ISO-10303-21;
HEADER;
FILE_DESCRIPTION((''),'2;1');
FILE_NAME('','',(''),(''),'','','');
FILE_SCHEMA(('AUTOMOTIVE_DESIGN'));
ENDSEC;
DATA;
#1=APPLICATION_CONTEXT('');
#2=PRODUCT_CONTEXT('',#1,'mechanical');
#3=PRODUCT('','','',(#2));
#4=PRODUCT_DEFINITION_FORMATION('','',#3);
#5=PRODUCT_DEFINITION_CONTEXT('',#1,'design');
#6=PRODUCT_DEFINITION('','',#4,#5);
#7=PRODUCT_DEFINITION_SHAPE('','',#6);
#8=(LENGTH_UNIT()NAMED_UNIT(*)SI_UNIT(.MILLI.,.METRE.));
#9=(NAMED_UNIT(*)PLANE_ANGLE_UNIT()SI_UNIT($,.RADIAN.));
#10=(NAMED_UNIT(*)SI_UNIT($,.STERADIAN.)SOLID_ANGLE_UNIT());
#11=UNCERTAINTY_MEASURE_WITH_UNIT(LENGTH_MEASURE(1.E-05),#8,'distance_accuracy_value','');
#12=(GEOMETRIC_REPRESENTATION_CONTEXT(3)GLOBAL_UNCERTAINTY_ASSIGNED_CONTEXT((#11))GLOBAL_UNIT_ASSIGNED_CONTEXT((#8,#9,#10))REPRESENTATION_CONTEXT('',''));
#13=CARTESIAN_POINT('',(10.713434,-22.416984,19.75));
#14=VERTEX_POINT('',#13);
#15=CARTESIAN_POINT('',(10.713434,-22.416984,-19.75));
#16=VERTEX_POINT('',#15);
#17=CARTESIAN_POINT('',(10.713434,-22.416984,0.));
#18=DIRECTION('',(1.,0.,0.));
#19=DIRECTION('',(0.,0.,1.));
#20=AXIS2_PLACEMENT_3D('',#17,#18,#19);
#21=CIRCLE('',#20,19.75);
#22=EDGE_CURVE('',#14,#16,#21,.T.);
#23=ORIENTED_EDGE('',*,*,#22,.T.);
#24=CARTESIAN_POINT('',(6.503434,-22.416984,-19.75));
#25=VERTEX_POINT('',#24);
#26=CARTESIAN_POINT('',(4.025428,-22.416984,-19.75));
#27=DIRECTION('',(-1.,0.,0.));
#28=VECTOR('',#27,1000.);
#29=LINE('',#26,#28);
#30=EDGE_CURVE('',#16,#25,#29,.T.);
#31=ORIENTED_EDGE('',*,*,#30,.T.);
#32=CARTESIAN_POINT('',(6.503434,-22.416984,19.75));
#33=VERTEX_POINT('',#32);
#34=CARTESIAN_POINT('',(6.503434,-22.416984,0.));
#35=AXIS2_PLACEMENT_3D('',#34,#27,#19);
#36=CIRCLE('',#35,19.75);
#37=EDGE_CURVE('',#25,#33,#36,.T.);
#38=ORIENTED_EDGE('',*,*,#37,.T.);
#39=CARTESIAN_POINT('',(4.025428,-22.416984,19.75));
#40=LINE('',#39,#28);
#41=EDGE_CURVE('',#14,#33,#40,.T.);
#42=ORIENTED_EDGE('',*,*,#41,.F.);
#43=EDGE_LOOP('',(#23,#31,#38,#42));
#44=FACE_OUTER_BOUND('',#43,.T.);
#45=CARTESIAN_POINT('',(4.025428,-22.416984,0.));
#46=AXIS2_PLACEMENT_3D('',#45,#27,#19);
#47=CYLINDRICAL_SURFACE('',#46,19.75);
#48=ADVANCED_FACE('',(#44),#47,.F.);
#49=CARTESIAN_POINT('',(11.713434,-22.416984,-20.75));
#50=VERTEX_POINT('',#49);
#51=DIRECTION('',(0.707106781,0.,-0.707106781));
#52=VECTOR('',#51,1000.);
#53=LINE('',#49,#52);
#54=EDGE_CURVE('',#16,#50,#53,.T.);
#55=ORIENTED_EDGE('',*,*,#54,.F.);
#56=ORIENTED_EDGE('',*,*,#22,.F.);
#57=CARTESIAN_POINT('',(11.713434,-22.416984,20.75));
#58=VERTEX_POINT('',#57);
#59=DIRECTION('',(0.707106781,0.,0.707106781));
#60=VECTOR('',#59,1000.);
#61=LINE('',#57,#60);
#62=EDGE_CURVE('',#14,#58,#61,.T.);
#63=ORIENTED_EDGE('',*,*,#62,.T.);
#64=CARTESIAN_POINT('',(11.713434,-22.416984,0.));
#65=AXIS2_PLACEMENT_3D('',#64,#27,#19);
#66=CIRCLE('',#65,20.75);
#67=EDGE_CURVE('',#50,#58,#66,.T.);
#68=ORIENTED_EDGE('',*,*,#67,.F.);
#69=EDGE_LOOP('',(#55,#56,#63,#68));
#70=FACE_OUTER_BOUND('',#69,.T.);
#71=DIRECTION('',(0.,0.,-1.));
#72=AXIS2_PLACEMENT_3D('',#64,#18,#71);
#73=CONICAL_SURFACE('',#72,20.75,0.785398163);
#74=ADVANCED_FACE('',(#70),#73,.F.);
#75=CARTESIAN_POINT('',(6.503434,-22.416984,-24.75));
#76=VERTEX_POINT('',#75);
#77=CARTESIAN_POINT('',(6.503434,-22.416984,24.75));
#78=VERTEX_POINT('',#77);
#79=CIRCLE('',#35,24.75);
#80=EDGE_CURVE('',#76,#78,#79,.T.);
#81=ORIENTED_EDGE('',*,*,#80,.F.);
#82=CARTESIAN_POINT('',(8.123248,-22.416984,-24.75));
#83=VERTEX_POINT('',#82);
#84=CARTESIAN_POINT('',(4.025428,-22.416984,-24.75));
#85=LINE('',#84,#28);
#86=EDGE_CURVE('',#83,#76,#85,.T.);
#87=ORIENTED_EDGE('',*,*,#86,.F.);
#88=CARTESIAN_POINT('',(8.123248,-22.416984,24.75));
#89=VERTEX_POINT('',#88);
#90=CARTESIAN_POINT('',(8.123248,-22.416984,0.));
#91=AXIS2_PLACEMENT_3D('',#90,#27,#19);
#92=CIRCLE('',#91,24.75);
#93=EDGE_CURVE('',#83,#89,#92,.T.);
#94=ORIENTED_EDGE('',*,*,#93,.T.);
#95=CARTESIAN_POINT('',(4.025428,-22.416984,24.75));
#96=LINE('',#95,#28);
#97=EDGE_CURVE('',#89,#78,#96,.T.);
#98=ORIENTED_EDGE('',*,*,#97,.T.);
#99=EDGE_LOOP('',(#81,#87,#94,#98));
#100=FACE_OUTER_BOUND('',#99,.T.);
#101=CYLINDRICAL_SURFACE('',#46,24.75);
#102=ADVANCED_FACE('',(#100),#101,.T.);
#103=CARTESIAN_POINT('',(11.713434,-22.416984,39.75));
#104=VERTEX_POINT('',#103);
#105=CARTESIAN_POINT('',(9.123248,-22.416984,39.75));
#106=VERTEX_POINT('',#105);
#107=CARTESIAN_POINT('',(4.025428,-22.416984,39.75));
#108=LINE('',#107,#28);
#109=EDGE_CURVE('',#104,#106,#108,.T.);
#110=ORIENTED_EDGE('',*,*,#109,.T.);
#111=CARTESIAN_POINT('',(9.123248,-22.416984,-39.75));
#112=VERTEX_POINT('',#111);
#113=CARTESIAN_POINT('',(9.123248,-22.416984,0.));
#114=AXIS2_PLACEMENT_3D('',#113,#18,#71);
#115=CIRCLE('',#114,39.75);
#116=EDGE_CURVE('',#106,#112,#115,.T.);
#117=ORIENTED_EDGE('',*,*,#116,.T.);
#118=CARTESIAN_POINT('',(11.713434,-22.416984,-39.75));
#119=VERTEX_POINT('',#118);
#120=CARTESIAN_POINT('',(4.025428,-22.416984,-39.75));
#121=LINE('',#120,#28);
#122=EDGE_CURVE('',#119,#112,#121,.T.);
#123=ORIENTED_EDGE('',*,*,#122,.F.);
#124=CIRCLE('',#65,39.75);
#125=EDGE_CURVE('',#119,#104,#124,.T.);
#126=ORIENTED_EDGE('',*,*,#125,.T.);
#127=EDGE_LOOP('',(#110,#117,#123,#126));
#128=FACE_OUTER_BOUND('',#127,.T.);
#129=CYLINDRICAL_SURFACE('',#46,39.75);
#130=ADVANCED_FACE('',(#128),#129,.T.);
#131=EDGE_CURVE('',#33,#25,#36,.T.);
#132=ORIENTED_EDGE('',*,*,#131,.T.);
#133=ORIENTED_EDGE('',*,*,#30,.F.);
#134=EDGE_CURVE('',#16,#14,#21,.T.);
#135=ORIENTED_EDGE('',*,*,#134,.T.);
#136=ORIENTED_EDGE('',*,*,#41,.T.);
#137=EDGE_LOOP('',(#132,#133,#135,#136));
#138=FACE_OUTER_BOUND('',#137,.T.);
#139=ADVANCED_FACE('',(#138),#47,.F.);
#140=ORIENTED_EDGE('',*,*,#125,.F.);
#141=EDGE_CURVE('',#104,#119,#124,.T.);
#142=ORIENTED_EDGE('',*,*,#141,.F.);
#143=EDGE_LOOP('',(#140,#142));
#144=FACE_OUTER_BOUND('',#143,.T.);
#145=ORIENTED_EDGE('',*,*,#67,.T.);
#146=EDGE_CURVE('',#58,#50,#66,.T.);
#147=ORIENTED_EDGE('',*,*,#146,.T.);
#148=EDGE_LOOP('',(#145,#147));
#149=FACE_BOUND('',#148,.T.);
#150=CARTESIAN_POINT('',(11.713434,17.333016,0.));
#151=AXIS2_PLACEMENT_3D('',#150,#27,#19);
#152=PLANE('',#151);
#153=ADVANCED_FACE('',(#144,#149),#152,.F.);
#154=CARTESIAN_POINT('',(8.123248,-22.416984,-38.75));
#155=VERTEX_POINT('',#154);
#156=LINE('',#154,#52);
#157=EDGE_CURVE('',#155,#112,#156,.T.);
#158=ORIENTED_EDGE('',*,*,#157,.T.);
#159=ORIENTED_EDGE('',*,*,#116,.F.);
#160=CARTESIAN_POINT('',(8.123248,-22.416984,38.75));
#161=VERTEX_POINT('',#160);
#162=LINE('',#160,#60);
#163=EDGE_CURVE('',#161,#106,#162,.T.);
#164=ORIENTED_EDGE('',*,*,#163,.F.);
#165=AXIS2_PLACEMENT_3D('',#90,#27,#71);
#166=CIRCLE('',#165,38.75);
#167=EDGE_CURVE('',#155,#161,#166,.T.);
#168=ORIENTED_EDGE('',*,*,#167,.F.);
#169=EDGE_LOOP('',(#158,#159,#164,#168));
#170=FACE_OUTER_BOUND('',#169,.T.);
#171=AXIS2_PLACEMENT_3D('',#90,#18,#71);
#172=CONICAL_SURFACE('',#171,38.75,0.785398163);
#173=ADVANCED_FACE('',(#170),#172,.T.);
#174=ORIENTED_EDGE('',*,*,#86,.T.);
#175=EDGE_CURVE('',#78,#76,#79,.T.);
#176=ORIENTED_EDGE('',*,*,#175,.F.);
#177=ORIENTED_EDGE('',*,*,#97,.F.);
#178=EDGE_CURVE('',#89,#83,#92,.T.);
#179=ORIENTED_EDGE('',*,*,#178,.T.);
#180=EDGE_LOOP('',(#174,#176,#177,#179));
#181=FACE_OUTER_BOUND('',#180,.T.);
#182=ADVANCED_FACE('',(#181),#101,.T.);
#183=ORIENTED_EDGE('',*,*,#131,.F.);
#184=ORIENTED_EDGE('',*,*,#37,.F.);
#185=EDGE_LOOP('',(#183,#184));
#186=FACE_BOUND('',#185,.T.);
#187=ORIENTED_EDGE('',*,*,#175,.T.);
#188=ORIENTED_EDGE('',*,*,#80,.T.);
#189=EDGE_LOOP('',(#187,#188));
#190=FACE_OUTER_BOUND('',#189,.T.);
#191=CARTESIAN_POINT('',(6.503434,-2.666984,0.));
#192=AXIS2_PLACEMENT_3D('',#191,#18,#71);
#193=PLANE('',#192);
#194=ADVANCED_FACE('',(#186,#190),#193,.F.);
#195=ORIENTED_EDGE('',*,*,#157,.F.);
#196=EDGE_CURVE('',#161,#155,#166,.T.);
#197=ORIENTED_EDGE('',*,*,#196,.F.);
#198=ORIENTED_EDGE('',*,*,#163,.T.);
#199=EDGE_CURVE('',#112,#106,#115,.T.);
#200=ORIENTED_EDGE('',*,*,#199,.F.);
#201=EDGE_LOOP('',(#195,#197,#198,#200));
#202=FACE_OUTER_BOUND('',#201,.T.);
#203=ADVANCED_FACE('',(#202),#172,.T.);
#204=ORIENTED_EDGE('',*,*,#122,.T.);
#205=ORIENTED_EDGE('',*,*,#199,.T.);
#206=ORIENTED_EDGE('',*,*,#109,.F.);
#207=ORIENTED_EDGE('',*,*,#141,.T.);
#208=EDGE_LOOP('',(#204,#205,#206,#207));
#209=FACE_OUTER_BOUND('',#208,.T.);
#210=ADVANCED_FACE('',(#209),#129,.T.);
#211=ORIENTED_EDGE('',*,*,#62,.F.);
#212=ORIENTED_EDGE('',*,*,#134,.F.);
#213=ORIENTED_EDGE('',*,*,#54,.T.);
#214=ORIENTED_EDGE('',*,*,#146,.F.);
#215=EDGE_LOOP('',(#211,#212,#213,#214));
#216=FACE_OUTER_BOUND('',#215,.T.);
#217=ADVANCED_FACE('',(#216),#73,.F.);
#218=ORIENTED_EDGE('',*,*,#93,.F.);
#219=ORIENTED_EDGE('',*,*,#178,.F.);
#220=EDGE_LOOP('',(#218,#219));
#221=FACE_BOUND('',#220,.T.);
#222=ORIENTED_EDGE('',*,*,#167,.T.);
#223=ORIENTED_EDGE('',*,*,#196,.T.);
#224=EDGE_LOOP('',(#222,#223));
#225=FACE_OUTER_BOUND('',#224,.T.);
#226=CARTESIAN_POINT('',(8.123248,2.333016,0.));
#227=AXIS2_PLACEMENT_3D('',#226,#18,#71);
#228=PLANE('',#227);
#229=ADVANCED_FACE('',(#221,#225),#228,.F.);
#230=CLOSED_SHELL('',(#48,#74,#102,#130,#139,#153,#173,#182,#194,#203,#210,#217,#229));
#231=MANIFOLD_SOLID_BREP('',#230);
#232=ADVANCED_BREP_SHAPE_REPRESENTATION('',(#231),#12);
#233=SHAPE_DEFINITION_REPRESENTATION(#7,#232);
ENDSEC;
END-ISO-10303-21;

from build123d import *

# Parameters (mm, degrees)
CHAMFER_1_SIZE = 1
CHAMFER_2_SIZE = 1


with BuildPart() as part:
    # 草图1 → 旋转1 (revolve)
    with BuildSketch(Plane.XY, mode=Mode.PRIVATE) as revolve_1_sk:
        Polygon((6.503433875, -2.666983759), (6.503433875, 2.333016241), (8.12324826, 2.333016241), (8.12324826, 17.333016241), (11.713433875, 17.333016241), (11.713433875, -2.666983759), align=None)
    revolve(revolve_1_sk.sketch.rotate(Axis((4.025427808, -22.416983759, 0), (1, 0, 0)), 90), axis=Axis((4.025427808, -22.416983759, 0), (1, 0, 0)))

    # 倒角1
    chamfer_1_edges = [part.edges().sort_by_distance(p)[0] for p in [
        (8.12324826, -22.416983759, -39.75),
    ]]
    chamfer(chamfer_1_edges, length=CHAMFER_1_SIZE)

    # 倒角2
    chamfer_2_edges = [part.edges().sort_by_distance(p)[0] for p in [
        (11.713433875, -22.416983759, -19.75),
    ]]
    chamfer(chamfer_2_edges, length=CHAMFER_2_SIZE)


solid = part.part
